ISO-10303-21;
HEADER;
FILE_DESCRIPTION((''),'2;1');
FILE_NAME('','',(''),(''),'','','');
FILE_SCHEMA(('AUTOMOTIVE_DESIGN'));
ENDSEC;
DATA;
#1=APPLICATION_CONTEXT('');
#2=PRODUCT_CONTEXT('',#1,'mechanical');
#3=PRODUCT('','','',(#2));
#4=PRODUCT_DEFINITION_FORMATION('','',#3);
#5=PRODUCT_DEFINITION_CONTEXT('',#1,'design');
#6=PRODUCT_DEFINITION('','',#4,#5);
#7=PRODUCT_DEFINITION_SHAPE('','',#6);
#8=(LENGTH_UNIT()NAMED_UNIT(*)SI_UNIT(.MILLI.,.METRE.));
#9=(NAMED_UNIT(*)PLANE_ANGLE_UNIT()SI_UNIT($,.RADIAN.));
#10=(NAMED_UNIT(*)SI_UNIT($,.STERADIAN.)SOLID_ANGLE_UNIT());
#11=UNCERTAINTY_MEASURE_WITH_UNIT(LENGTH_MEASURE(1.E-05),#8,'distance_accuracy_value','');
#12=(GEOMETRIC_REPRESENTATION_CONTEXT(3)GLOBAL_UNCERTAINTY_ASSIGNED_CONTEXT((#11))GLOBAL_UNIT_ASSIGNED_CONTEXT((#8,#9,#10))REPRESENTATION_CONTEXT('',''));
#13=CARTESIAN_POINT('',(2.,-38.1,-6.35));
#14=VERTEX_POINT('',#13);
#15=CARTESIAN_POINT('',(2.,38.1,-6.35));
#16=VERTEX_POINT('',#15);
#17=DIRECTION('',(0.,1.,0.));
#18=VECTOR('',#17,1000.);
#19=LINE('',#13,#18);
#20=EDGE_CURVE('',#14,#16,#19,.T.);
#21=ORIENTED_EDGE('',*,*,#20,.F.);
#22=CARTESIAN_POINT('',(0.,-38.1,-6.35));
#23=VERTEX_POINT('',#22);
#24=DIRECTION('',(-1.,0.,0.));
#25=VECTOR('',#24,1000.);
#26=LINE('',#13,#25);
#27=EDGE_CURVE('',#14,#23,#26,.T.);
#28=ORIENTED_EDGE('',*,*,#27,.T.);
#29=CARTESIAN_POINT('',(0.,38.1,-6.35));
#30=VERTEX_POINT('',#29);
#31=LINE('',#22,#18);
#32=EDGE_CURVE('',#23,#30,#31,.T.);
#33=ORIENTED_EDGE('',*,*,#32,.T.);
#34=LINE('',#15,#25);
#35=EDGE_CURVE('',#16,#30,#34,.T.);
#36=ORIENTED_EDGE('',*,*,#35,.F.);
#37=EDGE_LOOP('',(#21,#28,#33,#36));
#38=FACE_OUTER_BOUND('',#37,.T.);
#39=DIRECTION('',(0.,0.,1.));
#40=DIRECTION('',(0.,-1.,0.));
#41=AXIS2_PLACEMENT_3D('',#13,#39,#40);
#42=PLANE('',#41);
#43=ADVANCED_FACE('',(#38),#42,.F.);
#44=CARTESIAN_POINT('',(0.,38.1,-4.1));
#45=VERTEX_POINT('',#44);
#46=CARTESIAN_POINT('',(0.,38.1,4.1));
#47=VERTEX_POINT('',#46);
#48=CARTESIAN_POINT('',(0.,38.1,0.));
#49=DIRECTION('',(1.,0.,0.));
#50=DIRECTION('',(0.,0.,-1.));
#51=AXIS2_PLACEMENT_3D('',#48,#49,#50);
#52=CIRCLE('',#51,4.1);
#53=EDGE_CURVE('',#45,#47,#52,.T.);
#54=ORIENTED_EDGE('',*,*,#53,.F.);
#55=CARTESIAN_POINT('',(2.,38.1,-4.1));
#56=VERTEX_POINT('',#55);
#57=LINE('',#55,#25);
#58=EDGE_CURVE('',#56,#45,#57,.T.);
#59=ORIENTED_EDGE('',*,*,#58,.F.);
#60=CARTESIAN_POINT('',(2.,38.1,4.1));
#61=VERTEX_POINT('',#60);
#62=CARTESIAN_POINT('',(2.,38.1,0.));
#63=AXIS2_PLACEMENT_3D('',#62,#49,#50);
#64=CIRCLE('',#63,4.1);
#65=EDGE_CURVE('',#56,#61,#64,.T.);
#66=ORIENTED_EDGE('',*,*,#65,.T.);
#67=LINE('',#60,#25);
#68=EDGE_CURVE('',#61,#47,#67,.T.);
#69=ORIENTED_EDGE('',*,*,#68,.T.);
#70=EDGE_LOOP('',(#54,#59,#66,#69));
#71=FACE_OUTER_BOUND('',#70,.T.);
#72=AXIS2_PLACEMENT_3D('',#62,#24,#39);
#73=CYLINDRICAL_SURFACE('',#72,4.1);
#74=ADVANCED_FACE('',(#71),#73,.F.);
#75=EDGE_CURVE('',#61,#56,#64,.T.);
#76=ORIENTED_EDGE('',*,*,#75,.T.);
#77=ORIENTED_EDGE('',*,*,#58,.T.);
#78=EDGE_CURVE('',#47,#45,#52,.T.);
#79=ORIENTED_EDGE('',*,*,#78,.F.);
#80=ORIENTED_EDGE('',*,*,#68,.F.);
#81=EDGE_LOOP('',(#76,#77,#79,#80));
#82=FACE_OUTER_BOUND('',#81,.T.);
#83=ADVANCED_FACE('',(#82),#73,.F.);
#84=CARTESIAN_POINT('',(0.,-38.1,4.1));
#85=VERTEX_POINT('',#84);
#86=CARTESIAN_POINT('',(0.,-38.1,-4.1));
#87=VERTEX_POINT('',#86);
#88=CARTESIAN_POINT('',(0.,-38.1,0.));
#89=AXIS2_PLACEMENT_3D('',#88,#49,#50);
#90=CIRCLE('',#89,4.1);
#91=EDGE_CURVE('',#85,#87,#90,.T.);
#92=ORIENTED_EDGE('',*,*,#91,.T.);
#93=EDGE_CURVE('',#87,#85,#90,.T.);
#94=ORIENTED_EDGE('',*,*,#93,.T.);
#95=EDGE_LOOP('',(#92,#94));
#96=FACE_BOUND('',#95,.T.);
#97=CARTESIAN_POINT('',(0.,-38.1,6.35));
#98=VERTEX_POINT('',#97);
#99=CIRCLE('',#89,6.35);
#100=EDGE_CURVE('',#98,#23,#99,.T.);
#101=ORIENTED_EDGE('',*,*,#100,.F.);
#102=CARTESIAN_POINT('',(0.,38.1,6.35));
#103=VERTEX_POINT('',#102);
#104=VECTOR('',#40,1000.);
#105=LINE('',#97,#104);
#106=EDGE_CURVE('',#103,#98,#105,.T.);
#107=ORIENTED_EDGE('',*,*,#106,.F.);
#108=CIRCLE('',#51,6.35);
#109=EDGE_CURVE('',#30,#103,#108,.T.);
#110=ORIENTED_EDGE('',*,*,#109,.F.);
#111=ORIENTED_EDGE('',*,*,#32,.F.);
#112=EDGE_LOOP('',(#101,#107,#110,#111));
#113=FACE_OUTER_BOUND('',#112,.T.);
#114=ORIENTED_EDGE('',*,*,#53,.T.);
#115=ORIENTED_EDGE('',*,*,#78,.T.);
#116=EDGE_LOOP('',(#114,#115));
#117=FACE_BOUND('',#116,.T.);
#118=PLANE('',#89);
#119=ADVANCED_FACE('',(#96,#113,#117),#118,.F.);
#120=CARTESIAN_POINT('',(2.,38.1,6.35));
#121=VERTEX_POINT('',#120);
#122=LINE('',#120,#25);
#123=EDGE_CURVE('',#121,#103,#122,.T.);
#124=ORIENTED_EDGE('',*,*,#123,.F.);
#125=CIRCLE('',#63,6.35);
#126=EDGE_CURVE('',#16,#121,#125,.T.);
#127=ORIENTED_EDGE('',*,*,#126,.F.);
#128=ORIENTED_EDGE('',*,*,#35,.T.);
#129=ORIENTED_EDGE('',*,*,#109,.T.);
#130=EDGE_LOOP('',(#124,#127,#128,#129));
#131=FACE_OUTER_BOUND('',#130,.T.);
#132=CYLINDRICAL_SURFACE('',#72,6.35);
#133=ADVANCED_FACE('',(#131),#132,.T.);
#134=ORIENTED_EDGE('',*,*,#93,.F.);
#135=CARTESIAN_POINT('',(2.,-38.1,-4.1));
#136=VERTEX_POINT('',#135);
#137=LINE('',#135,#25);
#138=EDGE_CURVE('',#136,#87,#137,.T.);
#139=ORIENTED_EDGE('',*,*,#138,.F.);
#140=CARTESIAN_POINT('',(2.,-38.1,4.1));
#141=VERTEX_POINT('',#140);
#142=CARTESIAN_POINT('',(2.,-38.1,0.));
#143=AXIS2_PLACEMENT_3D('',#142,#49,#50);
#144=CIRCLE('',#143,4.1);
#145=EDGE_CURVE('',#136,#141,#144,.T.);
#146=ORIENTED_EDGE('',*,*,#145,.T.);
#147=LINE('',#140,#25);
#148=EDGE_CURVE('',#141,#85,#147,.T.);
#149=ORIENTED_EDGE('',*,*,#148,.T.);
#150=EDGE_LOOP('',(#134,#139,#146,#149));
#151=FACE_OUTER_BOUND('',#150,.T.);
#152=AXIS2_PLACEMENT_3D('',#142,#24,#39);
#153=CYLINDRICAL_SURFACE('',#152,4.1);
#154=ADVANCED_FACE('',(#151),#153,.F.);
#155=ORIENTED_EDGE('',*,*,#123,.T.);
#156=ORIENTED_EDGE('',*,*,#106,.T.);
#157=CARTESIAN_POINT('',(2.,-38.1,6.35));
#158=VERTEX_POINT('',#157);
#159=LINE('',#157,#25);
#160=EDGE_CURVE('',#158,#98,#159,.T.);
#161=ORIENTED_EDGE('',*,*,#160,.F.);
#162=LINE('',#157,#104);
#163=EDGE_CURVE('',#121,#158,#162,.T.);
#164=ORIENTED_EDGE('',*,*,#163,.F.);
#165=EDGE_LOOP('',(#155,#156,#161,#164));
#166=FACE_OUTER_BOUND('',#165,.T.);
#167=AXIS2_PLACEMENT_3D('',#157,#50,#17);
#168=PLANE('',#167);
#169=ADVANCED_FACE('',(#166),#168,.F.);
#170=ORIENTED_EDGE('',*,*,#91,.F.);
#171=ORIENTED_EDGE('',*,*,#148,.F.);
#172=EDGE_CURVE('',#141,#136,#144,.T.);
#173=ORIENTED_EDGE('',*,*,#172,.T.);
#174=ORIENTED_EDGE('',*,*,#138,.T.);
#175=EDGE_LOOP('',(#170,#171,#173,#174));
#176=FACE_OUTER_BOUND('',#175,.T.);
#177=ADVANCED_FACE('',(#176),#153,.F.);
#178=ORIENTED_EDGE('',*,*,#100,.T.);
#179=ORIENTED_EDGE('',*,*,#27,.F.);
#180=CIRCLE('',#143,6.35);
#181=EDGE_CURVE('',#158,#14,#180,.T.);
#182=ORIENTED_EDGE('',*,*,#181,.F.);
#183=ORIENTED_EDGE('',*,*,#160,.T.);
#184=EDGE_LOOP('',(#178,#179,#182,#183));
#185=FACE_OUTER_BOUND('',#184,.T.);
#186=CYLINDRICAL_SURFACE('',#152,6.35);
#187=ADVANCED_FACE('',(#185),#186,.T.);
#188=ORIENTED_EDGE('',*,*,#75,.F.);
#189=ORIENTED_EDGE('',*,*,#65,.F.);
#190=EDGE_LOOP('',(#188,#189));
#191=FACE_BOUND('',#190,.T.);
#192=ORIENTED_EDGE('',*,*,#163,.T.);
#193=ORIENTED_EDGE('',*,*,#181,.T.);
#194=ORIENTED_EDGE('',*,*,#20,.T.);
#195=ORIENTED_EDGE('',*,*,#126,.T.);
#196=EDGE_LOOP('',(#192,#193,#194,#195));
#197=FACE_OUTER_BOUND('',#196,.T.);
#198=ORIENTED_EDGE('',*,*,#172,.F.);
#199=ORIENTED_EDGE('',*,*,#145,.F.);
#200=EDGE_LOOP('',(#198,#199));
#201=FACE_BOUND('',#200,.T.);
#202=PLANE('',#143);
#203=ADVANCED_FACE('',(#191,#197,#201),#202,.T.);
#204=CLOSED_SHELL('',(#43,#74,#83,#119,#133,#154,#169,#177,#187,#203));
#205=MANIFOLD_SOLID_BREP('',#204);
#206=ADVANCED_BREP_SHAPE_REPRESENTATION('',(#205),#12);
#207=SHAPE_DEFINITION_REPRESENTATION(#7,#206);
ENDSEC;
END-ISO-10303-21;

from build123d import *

# Parameters (mm, degrees)
SKETCH1_R           = 4.1
BOSS_EXTRUDE1_DEPTH = 2


with BuildPart() as part:
    # Sketch1 → Boss-Extrude1 (new body)
    with BuildSketch(Plane(origin=(0, 0, 0), x_dir=(0, 0, -1), z_dir=(1, 0, 0))):
        with BuildLine():
            Line((-6.35, -38.1), (-6.35, 38.1))
            ThreePointArc((-6.35, 38.1), (0, 44.45), (6.35, 38.1))
            Line((6.35, 38.1), (6.35, -38.1))
            ThreePointArc((6.35, -38.1), (0, -44.45), (-6.35, -38.1))
        make_face()
        with Locations((0, 38.1)):
            Circle(SKETCH1_R, mode=Mode.SUBTRACT)
        with Locations((0, -38.1)):
            Circle(SKETCH1_R, mode=Mode.SUBTRACT)
    extrude(amount=BOSS_EXTRUDE1_DEPTH)


solid = part.part
